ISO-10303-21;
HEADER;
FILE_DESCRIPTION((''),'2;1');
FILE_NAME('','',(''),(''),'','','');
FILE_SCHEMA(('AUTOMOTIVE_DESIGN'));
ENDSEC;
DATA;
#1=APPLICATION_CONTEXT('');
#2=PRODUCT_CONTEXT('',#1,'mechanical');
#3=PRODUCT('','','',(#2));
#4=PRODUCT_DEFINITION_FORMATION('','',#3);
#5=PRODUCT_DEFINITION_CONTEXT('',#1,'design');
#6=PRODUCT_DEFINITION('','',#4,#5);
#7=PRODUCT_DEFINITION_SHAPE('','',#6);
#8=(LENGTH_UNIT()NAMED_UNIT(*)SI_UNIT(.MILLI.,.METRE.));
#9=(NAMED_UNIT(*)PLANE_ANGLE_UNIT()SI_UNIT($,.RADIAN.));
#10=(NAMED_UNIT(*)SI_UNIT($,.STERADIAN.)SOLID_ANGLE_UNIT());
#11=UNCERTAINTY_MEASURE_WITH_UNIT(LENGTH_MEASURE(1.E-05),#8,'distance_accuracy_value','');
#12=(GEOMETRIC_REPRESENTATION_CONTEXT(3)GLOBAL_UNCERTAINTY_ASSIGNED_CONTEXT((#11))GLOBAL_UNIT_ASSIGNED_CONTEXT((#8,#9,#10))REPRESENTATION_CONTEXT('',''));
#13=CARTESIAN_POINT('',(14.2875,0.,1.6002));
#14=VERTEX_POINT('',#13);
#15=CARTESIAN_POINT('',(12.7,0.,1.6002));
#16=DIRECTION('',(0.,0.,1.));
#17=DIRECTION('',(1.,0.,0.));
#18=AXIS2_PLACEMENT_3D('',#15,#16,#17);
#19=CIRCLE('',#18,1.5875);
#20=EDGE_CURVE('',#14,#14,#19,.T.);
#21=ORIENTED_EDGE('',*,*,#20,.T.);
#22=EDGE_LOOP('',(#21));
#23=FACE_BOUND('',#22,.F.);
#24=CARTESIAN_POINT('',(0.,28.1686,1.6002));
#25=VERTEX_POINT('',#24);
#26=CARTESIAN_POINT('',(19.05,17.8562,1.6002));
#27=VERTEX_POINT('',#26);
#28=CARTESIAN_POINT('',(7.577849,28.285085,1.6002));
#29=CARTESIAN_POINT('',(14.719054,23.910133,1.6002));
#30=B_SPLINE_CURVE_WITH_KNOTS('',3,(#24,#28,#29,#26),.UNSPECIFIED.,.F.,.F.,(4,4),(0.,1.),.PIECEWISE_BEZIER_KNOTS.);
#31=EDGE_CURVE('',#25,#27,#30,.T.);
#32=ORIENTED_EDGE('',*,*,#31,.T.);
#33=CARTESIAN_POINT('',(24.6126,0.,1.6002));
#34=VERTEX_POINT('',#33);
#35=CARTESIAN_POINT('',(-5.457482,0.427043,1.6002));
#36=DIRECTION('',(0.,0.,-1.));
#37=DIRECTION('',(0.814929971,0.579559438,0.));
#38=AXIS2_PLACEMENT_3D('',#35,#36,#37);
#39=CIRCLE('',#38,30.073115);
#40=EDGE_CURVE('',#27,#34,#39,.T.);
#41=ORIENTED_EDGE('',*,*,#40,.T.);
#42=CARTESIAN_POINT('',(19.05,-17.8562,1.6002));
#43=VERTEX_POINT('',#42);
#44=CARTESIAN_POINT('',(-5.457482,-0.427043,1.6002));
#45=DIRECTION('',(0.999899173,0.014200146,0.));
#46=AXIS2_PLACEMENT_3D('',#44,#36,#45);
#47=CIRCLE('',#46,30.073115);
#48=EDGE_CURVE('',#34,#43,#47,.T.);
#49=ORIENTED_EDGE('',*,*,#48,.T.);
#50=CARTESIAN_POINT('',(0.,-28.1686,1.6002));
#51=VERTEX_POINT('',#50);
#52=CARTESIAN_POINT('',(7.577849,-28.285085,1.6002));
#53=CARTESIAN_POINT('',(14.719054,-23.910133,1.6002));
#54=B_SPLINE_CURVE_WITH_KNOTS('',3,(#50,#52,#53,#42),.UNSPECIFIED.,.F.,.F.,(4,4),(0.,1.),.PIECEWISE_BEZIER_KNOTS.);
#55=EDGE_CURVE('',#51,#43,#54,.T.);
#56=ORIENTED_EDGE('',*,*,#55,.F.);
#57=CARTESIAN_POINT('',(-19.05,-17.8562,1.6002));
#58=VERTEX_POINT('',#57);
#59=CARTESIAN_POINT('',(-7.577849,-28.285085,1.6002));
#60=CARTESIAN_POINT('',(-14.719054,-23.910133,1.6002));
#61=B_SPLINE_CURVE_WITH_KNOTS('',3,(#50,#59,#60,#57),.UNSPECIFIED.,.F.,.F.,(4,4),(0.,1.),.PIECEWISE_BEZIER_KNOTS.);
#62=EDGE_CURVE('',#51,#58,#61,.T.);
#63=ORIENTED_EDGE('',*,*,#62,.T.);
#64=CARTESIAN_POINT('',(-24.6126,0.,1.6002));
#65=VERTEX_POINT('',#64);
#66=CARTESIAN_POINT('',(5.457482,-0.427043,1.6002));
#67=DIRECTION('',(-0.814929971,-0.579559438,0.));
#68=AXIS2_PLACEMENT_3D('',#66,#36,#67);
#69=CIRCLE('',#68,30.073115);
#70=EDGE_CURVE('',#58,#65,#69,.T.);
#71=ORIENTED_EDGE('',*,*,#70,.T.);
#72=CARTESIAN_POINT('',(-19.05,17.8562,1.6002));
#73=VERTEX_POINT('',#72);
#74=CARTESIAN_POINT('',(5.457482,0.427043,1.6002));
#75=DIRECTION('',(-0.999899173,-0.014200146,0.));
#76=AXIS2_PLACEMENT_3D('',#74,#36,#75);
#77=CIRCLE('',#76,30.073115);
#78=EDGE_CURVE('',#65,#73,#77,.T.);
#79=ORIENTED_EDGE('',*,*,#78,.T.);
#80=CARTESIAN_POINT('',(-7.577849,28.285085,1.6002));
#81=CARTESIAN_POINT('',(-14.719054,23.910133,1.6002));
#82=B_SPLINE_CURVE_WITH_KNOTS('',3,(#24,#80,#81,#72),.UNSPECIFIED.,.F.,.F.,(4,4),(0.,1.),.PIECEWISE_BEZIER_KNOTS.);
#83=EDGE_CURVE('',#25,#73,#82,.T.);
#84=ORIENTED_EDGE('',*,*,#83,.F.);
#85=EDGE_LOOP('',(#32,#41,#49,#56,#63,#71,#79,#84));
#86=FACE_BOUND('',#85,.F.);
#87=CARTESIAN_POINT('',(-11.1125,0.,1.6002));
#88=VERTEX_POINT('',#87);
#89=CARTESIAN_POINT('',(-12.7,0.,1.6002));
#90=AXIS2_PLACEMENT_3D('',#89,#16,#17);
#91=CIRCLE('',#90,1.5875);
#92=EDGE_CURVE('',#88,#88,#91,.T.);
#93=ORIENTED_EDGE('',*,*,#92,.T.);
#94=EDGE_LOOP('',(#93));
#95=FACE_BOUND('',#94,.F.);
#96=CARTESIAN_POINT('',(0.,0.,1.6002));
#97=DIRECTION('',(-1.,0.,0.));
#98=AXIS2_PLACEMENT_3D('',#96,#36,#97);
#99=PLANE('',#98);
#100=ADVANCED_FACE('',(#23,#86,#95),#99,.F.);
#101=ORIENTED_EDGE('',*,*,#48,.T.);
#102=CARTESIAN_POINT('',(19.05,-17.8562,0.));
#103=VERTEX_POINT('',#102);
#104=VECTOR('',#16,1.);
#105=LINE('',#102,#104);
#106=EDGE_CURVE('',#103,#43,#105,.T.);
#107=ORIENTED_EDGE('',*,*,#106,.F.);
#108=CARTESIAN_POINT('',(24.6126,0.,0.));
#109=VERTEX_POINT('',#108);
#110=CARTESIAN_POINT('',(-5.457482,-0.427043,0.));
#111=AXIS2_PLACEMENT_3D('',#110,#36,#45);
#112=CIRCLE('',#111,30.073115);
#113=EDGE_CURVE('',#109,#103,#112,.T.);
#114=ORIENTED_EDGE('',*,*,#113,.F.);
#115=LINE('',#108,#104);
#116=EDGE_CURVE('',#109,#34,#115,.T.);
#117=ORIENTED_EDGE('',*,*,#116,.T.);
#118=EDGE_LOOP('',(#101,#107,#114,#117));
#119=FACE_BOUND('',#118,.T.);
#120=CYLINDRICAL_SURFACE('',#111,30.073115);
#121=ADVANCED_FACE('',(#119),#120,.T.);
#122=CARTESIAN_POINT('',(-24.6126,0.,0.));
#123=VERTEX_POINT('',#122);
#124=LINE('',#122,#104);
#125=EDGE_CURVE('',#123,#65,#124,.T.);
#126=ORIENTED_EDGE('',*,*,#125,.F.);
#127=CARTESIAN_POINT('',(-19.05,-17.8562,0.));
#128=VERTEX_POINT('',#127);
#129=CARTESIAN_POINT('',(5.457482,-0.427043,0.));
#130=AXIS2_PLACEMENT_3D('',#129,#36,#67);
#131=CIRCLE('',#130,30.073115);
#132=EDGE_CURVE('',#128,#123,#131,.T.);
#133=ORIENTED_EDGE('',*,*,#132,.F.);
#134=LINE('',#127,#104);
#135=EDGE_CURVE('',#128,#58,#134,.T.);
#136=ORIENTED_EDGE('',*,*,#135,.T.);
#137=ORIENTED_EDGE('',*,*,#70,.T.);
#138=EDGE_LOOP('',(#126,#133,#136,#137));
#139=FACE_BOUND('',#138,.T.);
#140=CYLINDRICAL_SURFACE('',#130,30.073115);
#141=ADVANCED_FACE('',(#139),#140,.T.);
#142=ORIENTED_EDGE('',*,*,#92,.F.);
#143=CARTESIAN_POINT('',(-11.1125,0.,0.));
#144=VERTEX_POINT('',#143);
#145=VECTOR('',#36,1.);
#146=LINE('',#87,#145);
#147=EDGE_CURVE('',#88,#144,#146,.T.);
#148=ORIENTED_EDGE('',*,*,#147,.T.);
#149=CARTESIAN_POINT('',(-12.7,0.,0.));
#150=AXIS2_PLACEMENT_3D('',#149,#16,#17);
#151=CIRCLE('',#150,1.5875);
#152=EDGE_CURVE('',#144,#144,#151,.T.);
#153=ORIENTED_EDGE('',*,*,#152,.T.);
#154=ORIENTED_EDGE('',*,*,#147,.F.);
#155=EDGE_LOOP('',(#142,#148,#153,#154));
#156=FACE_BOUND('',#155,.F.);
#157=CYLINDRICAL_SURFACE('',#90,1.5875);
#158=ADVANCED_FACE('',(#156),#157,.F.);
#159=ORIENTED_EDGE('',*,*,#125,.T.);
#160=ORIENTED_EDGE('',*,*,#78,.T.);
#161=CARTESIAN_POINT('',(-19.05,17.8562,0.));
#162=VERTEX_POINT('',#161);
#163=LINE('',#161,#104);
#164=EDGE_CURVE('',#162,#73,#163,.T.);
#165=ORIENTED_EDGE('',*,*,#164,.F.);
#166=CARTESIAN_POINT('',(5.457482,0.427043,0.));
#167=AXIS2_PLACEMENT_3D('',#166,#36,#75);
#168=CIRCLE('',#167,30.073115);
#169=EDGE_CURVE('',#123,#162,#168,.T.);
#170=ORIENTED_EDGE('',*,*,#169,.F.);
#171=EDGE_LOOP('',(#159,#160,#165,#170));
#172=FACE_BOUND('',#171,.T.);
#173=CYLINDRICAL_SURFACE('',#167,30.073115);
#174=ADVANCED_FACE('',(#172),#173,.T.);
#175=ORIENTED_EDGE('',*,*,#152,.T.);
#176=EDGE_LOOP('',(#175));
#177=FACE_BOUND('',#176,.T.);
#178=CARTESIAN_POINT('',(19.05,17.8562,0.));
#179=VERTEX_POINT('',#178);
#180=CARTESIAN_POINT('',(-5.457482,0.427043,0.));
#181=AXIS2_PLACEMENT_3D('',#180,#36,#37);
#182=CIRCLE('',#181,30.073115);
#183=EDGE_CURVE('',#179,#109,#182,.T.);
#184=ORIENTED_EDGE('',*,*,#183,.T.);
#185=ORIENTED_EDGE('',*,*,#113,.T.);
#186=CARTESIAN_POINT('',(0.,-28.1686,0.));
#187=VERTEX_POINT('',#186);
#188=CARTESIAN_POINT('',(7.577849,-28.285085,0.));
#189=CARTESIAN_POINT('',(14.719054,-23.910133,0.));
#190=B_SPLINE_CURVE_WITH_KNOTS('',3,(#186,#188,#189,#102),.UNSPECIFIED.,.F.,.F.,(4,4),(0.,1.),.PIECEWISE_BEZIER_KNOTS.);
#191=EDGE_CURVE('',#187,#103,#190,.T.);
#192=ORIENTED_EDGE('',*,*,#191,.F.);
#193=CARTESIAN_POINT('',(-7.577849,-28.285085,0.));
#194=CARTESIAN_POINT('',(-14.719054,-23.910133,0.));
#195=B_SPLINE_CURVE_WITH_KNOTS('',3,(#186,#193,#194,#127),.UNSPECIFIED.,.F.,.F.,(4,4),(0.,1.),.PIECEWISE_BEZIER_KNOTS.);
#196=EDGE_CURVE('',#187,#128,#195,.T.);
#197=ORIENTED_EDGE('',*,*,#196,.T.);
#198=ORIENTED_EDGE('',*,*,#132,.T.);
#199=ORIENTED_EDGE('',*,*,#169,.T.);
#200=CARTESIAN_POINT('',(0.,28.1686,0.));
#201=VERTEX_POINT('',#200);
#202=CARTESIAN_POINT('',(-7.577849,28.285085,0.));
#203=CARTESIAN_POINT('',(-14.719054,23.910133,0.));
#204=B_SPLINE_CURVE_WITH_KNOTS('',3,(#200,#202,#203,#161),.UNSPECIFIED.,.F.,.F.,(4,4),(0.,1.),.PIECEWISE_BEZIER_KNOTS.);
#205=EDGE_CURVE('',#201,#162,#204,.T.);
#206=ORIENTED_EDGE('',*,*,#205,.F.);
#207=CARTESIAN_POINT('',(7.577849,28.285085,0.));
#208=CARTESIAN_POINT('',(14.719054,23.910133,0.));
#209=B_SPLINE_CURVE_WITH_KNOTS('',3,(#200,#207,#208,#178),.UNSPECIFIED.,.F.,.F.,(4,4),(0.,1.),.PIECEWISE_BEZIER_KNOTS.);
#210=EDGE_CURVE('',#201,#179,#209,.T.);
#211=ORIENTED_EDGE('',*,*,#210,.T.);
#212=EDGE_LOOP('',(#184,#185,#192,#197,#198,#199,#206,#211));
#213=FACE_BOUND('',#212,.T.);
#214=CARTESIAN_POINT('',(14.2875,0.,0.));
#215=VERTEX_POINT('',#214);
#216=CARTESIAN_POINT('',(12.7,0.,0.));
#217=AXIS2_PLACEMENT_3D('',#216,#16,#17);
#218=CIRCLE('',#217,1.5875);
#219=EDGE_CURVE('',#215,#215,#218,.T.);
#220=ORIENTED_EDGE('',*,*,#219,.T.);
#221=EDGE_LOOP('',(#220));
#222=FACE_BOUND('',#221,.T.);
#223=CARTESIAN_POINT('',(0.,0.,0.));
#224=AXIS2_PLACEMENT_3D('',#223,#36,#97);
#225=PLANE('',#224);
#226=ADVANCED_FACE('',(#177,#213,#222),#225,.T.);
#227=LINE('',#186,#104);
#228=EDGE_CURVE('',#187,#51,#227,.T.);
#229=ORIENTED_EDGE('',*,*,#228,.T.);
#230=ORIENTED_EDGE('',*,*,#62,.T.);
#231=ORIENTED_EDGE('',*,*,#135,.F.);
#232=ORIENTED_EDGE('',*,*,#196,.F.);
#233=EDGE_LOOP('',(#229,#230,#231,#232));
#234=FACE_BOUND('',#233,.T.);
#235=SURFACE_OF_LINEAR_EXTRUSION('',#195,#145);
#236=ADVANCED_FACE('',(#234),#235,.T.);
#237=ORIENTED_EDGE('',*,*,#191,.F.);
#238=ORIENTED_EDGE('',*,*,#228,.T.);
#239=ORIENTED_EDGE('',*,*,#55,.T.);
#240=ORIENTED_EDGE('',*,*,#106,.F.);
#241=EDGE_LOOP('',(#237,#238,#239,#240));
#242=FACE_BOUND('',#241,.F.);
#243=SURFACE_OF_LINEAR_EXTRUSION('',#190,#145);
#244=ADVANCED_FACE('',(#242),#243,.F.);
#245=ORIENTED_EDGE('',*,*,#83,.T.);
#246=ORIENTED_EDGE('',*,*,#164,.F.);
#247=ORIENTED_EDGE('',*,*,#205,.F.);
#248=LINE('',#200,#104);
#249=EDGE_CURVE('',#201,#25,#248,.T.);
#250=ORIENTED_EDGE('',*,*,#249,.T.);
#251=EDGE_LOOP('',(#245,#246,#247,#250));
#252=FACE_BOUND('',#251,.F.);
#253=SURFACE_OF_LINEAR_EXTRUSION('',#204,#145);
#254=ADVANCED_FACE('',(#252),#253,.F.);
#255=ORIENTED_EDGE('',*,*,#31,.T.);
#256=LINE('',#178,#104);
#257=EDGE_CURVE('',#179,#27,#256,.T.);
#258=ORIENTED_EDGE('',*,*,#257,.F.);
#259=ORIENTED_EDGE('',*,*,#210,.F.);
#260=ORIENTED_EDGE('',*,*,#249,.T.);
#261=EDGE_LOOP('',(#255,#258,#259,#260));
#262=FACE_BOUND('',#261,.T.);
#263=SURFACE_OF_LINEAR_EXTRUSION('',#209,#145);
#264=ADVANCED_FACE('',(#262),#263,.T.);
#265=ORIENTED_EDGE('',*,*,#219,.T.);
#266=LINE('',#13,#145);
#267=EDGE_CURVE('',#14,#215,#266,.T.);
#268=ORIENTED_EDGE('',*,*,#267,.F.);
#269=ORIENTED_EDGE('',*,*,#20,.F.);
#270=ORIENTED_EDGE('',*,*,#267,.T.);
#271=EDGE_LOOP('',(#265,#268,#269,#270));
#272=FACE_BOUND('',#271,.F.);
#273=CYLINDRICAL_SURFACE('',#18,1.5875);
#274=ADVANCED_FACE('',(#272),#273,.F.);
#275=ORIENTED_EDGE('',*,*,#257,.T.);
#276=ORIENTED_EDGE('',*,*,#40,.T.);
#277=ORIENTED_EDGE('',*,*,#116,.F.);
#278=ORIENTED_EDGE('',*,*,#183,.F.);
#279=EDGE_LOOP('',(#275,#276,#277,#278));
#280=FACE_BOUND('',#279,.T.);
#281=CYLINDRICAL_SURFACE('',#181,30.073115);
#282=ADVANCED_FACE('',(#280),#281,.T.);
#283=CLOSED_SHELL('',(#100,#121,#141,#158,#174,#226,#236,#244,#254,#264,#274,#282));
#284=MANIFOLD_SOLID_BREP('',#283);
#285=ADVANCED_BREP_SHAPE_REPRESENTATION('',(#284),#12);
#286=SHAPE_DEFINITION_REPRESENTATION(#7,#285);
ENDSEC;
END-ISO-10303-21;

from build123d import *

# Parameters (mm, degrees)
BOSS_EXTRUDE1_DEPTH = 1.6002
SKETCH2_R           = 1.5875
CUT_EXTRUDE1_DEPTH  = 1.6002


with BuildPart() as part:
    # Sketch1 → Boss-Extrude1 (new body)
    with BuildSketch(Plane.XY):
        with BuildLine():
            add(Edge.make_bspline(
                [(0, -28.1686), (-7.577848525, -28.285084622), (-14.719054348, -23.91013337), (-19.05, -17.8562)],
                knots=[0, 0, 0, 0, 1, 1, 1, 1], degree=3))
            ThreePointArc((-19.05, -17.8562), (-23.254686005, -9.371516124), (-24.6126, 0))
            ThreePointArc((-24.6126, 0), (-23.254686005, 9.371516124), (-19.05, 17.8562))
            add(Edge.make_bspline(
                [(0, 28.1686), (-7.577848525, 28.285084622), (-14.719054348, 23.91013337), (-19.05, 17.8562)],
                knots=[0, 0, 0, 0, 1, 1, 1, 1], degree=3))
            add(Edge.make_bspline(
                [(0, 28.1686), (7.577848525, 28.285084622), (14.719054348, 23.91013337), (19.05, 17.8562)],
                knots=[0, 0, 0, 0, 1, 1, 1, 1], degree=3))
            ThreePointArc((19.05, 17.8562), (23.254686005, 9.371516124), (24.6126, 0))
            ThreePointArc((24.6126, 0), (23.254686005, -9.371516124), (19.05, -17.8562))
            add(Edge.make_bspline(
                [(0, -28.1686), (7.577848525, -28.285084622), (14.719054348, -23.91013337), (19.05, -17.8562)],
                knots=[0, 0, 0, 0, 1, 1, 1, 1], degree=3))
        make_face()
    extrude(amount=BOSS_EXTRUDE1_DEPTH)

    # Sketch2 → Cut-Extrude1 (cut)
    with BuildSketch(Plane.XY.offset(1.6002)):
        with Locations((-12.7, 0)):
            Circle(SKETCH2_R)
        with Locations((12.7, 0)):
            Circle(SKETCH2_R)
    extrude(amount=-CUT_EXTRUDE1_DEPTH, mode=Mode.SUBTRACT)


solid = part.part
